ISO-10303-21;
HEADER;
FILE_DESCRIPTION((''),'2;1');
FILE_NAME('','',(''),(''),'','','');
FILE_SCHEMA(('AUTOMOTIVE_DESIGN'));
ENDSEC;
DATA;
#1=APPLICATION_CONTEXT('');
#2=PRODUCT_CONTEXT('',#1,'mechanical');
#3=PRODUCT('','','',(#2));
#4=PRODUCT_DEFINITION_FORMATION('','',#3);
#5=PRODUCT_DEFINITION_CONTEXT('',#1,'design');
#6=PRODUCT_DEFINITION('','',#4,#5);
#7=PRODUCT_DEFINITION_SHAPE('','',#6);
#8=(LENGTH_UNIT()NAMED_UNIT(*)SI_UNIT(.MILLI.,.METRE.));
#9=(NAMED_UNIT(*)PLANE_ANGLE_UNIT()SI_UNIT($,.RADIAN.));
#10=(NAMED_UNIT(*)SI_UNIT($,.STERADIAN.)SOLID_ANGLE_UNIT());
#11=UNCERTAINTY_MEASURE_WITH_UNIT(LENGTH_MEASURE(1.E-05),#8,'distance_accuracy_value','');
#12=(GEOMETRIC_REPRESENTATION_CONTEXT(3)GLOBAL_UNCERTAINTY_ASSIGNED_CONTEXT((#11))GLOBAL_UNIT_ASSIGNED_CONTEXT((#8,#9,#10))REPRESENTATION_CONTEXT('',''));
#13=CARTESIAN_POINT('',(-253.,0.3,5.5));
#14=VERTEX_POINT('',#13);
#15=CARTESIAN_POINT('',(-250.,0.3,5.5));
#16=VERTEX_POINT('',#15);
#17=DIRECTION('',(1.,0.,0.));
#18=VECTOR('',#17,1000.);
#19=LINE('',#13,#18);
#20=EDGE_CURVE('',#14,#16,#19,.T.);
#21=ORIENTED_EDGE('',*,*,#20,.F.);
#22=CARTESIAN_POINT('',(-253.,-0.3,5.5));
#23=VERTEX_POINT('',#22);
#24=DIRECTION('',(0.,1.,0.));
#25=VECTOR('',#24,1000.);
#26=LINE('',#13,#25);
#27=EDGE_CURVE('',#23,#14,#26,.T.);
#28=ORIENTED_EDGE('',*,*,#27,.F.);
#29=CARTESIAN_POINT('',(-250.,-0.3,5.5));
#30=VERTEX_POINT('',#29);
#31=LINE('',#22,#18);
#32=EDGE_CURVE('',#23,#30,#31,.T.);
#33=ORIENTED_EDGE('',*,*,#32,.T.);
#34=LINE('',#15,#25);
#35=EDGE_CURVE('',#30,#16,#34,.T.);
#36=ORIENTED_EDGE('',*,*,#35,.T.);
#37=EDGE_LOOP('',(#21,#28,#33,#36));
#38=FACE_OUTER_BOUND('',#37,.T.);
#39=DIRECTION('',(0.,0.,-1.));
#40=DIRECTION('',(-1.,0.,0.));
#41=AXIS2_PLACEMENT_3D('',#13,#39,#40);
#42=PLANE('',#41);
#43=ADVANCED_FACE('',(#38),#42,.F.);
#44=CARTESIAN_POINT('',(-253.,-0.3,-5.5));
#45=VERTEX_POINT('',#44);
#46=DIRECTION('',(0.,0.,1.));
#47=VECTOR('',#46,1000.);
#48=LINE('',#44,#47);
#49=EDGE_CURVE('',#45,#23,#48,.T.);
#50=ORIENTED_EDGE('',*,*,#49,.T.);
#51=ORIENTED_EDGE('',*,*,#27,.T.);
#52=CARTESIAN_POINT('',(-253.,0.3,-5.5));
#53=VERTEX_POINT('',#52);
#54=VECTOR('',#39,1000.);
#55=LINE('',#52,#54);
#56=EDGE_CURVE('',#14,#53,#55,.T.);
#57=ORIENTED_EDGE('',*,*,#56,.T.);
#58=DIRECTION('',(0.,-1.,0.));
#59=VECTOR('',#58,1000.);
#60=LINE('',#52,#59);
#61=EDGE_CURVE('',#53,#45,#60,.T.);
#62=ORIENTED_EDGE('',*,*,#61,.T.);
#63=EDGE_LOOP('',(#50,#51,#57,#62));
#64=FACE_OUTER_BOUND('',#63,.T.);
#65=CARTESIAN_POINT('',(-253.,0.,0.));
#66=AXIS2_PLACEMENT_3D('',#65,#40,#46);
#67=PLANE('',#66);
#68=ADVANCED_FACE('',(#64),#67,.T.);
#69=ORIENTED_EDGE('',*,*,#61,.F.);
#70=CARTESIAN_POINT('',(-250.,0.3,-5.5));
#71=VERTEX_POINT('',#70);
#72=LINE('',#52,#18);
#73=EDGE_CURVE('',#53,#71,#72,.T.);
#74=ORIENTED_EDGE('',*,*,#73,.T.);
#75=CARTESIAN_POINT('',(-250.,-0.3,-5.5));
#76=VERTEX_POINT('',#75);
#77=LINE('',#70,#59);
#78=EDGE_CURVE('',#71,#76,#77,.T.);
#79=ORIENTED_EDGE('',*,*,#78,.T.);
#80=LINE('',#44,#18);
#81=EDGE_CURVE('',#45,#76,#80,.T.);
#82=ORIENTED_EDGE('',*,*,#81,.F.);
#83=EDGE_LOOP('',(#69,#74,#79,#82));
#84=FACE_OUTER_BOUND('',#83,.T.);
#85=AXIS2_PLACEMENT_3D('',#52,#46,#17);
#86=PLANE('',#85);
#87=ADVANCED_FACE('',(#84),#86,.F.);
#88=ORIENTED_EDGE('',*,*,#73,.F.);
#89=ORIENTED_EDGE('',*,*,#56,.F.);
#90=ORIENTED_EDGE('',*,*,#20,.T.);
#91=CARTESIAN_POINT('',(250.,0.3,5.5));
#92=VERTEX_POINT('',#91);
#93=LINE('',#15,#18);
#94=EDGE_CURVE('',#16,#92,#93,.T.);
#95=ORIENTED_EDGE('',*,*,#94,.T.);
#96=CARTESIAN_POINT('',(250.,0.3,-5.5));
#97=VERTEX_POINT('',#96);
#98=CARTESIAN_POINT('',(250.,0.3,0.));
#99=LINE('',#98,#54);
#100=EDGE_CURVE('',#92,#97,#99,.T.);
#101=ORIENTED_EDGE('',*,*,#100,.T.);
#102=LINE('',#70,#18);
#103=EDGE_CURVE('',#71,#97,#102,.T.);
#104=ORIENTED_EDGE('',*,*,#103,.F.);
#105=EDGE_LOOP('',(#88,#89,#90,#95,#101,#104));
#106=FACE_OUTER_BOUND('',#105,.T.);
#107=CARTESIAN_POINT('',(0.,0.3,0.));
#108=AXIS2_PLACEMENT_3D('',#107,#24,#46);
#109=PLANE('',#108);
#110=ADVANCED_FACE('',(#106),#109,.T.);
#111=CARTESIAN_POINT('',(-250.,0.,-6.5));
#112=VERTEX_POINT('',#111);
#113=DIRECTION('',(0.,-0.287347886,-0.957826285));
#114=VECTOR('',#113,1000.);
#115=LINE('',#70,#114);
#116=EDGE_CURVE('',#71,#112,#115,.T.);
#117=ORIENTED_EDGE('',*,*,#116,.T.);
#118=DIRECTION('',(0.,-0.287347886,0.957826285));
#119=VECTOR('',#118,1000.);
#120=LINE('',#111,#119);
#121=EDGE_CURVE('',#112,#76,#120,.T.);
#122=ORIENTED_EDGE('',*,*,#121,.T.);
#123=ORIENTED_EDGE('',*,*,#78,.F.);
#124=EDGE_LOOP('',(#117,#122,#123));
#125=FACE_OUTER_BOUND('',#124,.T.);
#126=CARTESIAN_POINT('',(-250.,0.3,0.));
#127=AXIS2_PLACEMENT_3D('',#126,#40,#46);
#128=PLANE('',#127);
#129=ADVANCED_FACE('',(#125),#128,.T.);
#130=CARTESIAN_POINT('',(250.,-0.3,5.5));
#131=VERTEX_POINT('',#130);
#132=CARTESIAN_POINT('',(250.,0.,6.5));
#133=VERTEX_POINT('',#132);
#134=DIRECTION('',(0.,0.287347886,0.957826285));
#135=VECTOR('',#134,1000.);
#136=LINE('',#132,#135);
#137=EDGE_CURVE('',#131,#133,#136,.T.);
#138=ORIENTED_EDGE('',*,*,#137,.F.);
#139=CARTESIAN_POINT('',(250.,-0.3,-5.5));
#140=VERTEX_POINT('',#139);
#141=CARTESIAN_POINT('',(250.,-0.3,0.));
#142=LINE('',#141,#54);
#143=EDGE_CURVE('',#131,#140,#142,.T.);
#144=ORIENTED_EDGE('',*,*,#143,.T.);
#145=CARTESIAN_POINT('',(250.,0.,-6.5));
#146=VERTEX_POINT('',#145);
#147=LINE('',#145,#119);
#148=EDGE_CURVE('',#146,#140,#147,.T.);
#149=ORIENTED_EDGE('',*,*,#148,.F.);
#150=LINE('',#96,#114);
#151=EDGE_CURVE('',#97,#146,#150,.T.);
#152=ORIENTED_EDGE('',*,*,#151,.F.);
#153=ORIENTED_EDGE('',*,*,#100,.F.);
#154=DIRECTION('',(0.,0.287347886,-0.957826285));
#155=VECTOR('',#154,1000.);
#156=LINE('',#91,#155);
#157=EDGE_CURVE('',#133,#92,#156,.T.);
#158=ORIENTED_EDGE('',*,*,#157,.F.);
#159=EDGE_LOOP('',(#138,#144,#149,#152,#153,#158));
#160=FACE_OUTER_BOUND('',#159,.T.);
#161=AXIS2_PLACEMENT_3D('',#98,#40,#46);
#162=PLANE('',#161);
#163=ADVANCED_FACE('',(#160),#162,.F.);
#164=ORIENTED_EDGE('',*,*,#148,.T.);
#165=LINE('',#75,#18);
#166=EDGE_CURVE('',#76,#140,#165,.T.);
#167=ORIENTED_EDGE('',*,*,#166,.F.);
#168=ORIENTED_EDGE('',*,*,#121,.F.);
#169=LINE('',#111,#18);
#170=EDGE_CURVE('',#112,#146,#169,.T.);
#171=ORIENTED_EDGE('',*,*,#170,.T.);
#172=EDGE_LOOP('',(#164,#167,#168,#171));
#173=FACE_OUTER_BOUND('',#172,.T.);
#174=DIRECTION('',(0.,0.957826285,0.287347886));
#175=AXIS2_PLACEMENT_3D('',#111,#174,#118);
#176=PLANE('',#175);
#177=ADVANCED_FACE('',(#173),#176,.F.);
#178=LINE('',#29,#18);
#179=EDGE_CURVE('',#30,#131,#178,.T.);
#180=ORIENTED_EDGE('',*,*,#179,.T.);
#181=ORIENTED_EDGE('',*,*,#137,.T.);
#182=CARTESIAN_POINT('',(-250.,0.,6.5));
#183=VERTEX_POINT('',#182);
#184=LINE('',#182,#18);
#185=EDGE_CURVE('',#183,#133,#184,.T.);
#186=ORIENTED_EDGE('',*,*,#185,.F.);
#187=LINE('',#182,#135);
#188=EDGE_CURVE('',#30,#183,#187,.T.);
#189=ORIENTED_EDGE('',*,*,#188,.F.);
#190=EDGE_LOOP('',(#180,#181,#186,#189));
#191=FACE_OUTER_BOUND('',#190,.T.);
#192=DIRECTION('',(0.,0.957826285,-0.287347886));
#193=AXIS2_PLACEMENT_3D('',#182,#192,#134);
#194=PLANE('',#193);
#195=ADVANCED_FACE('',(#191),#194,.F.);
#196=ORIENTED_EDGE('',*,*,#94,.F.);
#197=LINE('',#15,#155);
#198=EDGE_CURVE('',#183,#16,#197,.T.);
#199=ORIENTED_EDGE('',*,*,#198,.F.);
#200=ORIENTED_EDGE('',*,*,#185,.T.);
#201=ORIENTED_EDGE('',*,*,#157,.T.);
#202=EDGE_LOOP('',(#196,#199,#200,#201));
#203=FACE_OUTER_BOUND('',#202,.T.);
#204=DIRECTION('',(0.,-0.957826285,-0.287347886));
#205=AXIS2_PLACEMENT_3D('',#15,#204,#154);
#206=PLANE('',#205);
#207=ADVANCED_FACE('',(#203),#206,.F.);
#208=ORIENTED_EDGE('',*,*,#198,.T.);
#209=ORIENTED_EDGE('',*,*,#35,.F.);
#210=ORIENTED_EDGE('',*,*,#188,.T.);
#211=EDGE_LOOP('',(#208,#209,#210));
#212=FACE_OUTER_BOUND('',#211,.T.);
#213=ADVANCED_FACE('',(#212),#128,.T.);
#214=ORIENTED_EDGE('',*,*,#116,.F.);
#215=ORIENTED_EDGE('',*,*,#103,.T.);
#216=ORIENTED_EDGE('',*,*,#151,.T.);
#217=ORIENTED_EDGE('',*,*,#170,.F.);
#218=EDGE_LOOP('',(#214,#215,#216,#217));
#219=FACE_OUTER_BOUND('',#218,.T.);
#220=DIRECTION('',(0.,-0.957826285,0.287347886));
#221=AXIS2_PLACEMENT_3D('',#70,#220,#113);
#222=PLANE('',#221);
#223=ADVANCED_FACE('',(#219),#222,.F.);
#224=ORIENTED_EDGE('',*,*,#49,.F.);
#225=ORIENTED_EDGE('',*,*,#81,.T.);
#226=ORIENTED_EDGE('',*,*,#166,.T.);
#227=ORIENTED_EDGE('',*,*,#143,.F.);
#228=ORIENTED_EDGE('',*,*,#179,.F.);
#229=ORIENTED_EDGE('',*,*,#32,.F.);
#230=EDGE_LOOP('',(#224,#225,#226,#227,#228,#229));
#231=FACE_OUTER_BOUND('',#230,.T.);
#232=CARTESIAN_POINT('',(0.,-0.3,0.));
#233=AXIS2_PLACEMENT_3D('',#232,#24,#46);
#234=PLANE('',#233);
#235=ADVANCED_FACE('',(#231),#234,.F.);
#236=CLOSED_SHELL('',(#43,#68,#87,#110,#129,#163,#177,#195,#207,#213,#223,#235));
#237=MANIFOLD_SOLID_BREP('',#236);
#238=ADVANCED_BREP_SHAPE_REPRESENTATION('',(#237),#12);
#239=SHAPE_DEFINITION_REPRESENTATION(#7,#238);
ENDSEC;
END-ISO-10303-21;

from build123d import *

# Parameters (mm, degrees)
SKETCH1_W               = 500
SKETCH1_H               = 13
BOSS_EXTRUDE1_DEPTH     = 0.3
CUT_EXTRUDE1_DEPTH      = 251.084665663
CUT_EXTRUDE1_DEPTH_BACK = 251.084665663
SKETCH3_W               = 11
SKETCH3_H               = 0.6
BOSS_EXTRUDE2_DEPTH     = 3


with BuildPart() as part:
    # Sketch1 → Boss-Extrude1 (new, symmetric)
    with BuildSketch(Plane(origin=(0, 0, 0), x_dir=(1, 0, 0), z_dir=(0, 1, 0))):
        Rectangle(SKETCH1_W, SKETCH1_H)
    extrude(amount=BOSS_EXTRUDE1_DEPTH, both=True)

    # Sketch2 → Cut-Extrude1 (cut, two sides: drawn at the far end of the back side and taken through both)
    with BuildSketch(Plane(origin=(0, 0, 0), x_dir=(0, 0, -1), z_dir=(1, 0, 0)).offset(-CUT_EXTRUDE1_DEPTH_BACK)):
        Polygon((5.5, 0.3), (6.5, 0), (5.5, -0.3), (7, -0.3), (7, 0.3), align=None)
        Polygon((-7, 0.3), (-5.5, 0.3), (-6.5, 0), (-5.5, -0.3), (-7, -0.3), align=None)
    extrude(amount=CUT_EXTRUDE1_DEPTH + CUT_EXTRUDE1_DEPTH_BACK, mode=Mode.SUBTRACT)

    # Sketch3 → Boss-Extrude2 (add)
    with BuildSketch(Plane.ZY.offset(250)):
        Rectangle(SKETCH3_W, SKETCH3_H)
    extrude(amount=BOSS_EXTRUDE2_DEPTH)


solid = part.part
